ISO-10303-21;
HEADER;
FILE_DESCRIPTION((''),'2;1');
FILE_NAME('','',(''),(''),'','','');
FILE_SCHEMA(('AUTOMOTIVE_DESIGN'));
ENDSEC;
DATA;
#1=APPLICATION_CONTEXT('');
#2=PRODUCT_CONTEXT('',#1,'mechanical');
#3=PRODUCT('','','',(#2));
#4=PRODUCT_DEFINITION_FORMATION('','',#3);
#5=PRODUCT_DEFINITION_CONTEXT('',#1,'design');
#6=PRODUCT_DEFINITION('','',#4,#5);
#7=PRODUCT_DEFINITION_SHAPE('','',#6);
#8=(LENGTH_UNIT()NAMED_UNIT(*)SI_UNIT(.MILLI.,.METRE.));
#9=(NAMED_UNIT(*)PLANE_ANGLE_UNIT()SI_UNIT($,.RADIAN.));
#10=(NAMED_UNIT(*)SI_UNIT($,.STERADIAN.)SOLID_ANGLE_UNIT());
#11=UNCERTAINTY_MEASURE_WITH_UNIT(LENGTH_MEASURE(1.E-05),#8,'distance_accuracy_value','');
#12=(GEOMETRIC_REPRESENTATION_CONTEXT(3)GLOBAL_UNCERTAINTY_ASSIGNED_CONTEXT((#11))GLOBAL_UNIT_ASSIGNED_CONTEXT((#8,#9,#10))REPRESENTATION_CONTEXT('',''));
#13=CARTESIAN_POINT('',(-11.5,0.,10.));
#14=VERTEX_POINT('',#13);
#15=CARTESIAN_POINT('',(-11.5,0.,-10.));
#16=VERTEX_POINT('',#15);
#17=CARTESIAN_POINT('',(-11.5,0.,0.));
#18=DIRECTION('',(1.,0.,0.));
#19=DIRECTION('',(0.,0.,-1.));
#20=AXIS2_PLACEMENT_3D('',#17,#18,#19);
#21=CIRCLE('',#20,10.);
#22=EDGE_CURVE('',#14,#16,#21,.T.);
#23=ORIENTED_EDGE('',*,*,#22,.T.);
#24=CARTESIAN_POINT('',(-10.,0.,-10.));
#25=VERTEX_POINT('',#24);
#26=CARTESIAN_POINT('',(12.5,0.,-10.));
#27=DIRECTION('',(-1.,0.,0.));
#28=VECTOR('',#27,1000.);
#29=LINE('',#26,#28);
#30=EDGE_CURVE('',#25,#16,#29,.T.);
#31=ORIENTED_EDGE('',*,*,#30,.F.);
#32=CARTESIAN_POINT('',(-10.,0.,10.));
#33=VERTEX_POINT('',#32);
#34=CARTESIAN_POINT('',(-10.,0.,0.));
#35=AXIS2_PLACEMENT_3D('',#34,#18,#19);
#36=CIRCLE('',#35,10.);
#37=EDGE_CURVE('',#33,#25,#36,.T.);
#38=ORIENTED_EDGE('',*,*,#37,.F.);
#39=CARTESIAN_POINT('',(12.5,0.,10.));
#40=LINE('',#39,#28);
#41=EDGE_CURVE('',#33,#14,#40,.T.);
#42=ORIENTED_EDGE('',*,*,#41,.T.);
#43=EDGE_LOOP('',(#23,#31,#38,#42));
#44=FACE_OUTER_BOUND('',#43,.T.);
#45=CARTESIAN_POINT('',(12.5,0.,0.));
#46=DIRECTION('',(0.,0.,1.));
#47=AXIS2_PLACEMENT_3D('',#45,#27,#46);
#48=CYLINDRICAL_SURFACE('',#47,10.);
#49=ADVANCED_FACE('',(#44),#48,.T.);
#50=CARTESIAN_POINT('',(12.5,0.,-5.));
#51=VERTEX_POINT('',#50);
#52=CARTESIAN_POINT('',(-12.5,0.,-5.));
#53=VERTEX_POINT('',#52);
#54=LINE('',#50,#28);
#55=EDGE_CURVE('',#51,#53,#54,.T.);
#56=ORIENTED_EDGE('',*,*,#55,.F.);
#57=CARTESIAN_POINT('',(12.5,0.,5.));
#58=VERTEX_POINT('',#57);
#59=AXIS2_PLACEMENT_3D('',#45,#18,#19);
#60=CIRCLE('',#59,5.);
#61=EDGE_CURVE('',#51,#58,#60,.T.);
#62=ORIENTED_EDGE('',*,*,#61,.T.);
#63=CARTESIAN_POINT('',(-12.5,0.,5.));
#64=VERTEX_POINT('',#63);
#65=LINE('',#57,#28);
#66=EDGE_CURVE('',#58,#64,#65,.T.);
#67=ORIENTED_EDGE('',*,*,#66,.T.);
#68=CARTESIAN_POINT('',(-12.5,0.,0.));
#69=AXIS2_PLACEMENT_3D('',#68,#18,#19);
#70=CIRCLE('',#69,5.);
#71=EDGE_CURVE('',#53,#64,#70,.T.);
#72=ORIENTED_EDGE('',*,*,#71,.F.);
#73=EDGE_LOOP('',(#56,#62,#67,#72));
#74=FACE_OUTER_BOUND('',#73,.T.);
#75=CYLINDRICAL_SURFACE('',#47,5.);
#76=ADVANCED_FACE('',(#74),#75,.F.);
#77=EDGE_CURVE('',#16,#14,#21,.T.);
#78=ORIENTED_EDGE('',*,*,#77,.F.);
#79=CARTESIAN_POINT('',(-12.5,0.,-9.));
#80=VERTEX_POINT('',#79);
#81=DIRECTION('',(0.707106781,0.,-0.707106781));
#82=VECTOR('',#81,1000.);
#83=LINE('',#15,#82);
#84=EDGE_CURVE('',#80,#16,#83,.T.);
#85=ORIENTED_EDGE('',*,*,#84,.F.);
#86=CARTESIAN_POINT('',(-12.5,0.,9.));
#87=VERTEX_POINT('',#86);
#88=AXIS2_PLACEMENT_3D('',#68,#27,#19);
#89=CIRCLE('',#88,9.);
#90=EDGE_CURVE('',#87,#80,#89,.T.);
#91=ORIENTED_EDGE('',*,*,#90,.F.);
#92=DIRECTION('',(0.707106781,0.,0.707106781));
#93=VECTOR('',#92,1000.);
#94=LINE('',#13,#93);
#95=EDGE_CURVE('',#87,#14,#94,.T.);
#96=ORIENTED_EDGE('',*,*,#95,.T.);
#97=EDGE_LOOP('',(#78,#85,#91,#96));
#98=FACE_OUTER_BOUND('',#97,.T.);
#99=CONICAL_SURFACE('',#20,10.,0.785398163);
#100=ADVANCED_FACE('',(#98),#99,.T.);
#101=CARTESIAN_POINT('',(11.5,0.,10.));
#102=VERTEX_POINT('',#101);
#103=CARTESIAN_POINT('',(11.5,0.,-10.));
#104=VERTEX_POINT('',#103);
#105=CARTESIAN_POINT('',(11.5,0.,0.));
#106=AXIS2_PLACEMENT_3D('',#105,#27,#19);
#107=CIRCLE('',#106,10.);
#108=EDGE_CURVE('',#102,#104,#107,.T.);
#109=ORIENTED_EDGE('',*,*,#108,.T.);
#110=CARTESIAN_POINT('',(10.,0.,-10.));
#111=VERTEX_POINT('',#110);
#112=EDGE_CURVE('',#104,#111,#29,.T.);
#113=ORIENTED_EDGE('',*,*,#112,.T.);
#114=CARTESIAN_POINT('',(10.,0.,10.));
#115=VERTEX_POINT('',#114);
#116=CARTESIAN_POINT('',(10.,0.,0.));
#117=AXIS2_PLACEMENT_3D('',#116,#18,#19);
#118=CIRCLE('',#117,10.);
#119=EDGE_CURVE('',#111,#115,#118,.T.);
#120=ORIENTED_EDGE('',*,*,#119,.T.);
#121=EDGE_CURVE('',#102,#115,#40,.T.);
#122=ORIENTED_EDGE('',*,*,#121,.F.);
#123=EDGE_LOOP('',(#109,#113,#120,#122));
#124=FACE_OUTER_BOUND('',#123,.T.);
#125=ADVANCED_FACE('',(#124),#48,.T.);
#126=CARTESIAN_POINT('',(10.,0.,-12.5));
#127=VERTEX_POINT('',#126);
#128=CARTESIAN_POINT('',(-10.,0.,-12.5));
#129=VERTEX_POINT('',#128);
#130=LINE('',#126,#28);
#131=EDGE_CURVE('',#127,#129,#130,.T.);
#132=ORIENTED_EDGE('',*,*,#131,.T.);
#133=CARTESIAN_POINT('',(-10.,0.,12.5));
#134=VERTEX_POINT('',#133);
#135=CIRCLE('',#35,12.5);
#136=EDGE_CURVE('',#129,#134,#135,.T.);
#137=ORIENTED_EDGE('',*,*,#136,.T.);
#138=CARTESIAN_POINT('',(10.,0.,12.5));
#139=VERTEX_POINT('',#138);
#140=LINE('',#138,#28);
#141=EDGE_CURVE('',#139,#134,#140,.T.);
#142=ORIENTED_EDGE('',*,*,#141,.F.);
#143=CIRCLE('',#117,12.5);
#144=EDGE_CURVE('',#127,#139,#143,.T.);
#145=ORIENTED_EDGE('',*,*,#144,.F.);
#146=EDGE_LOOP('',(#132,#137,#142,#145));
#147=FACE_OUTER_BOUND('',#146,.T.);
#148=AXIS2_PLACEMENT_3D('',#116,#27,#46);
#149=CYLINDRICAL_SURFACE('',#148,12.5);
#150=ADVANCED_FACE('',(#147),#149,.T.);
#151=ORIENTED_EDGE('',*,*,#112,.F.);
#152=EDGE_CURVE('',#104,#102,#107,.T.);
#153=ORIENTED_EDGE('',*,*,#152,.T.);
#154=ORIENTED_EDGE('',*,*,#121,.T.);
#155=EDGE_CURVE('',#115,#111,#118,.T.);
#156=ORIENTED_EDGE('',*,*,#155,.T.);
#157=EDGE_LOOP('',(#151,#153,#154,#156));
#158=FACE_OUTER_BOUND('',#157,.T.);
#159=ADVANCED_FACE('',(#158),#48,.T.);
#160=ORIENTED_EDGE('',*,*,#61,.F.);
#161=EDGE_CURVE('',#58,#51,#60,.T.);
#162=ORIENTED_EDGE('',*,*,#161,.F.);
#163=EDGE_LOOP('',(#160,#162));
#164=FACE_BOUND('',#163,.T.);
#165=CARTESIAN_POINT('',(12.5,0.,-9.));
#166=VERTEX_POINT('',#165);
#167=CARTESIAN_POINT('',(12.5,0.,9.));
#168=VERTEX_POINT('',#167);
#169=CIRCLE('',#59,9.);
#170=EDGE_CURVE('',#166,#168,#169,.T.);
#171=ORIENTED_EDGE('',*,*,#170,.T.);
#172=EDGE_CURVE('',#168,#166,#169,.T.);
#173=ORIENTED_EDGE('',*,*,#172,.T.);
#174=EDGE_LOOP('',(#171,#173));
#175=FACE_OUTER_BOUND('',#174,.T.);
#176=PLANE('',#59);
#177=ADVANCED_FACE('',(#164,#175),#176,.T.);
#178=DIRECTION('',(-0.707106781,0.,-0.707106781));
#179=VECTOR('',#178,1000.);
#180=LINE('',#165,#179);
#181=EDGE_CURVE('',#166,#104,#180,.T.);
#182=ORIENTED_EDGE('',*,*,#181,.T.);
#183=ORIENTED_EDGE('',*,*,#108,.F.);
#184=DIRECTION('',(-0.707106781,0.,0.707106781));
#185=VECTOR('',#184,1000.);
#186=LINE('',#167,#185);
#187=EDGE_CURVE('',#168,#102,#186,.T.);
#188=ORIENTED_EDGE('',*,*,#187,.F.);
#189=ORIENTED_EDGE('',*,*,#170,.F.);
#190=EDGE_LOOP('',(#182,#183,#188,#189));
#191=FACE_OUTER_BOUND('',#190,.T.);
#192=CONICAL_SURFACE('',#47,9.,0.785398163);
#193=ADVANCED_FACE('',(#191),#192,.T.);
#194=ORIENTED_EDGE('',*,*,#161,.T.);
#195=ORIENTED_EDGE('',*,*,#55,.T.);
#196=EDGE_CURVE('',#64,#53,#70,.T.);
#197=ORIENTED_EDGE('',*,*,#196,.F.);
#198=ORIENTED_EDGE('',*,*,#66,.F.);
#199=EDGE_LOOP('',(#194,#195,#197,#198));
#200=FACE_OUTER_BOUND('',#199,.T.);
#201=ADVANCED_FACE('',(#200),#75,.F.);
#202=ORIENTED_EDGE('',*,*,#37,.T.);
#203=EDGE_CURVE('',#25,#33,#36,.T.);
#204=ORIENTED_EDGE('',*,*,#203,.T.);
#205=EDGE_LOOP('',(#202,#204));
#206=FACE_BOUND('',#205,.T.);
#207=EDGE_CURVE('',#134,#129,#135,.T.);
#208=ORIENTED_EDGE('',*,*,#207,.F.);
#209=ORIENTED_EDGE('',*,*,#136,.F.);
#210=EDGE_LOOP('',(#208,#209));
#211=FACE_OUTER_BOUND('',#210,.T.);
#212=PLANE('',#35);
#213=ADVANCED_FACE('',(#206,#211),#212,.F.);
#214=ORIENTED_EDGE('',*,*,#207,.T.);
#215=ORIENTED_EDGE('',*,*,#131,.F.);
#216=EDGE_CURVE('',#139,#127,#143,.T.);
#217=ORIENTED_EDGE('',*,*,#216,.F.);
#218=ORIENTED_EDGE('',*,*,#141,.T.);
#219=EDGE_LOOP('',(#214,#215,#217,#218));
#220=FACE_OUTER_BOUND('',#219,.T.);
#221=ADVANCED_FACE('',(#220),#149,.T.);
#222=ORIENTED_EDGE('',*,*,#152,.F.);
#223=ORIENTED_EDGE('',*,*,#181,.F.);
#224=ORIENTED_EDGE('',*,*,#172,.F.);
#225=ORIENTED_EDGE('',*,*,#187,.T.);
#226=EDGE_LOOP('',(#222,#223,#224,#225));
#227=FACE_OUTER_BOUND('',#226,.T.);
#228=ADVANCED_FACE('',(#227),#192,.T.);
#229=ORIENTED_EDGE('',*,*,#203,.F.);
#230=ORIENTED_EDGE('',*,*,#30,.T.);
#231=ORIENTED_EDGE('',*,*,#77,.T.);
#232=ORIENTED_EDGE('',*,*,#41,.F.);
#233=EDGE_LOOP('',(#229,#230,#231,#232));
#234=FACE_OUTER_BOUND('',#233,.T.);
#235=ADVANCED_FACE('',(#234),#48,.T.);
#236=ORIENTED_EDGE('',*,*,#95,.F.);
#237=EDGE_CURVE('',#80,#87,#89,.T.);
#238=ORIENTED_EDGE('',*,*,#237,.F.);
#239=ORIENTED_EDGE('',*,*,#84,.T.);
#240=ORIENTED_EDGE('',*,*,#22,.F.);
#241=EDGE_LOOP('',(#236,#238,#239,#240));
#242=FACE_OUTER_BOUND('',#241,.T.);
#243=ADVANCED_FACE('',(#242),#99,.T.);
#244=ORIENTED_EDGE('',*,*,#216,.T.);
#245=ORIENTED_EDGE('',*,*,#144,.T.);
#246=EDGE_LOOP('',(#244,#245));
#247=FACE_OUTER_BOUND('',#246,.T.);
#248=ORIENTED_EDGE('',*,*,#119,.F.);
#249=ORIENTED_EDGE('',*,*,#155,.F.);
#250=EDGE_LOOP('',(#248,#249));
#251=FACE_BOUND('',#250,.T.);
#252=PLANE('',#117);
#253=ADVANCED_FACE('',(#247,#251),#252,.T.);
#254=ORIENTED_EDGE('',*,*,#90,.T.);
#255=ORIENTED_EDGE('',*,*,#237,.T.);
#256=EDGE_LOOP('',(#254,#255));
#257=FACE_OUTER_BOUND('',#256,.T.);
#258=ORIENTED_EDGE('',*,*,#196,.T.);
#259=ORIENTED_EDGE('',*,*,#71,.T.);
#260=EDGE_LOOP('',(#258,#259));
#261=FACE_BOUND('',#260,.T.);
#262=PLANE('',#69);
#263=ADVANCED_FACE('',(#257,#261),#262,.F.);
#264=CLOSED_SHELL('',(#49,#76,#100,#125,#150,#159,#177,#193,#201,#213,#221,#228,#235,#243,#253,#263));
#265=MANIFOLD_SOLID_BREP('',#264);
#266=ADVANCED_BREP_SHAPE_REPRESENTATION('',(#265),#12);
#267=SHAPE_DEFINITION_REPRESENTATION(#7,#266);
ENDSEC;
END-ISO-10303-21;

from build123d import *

# Parameters (mm, degrees)
SKETCH_1_R      = 10
SKETCH_1_R_2    = 5
EXTRUDE_1_DEPTH = 12.5
SKETCH_2_R      = 12.5
SKETCH_2_R_2    = 10
EXTRUDE_2_DEPTH = 10
CHAMFER_1_SIZE  = 1


with BuildPart() as part:
    # 草图1 → 凸台-拉伸1 (new, symmetric)
    with BuildSketch(Plane(origin=(0, 0, 0), x_dir=(0, 0, -1), z_dir=(1, 0, 0))):
        Circle(SKETCH_1_R)
        Circle(SKETCH_1_R_2, mode=Mode.SUBTRACT)
    extrude(amount=EXTRUDE_1_DEPTH, both=True)

    # 草图2 → 凸台-拉伸2 (add, symmetric)
    with BuildSketch(Plane(origin=(0, 0, 0), x_dir=(0, 0, -1), z_dir=(1, 0, 0))):
        Circle(SKETCH_2_R)
        Circle(SKETCH_2_R_2, mode=Mode.SUBTRACT)
    extrude(amount=EXTRUDE_2_DEPTH, both=True)

    # 倒角1
    chamfer_1_edges = [part.edges().sort_by_distance(p)[0] for p in [
        (-12.5, 0, 10),
        (12.5, 0, 10),
    ]]
    chamfer(chamfer_1_edges, length=CHAMFER_1_SIZE)


solid = part.part
